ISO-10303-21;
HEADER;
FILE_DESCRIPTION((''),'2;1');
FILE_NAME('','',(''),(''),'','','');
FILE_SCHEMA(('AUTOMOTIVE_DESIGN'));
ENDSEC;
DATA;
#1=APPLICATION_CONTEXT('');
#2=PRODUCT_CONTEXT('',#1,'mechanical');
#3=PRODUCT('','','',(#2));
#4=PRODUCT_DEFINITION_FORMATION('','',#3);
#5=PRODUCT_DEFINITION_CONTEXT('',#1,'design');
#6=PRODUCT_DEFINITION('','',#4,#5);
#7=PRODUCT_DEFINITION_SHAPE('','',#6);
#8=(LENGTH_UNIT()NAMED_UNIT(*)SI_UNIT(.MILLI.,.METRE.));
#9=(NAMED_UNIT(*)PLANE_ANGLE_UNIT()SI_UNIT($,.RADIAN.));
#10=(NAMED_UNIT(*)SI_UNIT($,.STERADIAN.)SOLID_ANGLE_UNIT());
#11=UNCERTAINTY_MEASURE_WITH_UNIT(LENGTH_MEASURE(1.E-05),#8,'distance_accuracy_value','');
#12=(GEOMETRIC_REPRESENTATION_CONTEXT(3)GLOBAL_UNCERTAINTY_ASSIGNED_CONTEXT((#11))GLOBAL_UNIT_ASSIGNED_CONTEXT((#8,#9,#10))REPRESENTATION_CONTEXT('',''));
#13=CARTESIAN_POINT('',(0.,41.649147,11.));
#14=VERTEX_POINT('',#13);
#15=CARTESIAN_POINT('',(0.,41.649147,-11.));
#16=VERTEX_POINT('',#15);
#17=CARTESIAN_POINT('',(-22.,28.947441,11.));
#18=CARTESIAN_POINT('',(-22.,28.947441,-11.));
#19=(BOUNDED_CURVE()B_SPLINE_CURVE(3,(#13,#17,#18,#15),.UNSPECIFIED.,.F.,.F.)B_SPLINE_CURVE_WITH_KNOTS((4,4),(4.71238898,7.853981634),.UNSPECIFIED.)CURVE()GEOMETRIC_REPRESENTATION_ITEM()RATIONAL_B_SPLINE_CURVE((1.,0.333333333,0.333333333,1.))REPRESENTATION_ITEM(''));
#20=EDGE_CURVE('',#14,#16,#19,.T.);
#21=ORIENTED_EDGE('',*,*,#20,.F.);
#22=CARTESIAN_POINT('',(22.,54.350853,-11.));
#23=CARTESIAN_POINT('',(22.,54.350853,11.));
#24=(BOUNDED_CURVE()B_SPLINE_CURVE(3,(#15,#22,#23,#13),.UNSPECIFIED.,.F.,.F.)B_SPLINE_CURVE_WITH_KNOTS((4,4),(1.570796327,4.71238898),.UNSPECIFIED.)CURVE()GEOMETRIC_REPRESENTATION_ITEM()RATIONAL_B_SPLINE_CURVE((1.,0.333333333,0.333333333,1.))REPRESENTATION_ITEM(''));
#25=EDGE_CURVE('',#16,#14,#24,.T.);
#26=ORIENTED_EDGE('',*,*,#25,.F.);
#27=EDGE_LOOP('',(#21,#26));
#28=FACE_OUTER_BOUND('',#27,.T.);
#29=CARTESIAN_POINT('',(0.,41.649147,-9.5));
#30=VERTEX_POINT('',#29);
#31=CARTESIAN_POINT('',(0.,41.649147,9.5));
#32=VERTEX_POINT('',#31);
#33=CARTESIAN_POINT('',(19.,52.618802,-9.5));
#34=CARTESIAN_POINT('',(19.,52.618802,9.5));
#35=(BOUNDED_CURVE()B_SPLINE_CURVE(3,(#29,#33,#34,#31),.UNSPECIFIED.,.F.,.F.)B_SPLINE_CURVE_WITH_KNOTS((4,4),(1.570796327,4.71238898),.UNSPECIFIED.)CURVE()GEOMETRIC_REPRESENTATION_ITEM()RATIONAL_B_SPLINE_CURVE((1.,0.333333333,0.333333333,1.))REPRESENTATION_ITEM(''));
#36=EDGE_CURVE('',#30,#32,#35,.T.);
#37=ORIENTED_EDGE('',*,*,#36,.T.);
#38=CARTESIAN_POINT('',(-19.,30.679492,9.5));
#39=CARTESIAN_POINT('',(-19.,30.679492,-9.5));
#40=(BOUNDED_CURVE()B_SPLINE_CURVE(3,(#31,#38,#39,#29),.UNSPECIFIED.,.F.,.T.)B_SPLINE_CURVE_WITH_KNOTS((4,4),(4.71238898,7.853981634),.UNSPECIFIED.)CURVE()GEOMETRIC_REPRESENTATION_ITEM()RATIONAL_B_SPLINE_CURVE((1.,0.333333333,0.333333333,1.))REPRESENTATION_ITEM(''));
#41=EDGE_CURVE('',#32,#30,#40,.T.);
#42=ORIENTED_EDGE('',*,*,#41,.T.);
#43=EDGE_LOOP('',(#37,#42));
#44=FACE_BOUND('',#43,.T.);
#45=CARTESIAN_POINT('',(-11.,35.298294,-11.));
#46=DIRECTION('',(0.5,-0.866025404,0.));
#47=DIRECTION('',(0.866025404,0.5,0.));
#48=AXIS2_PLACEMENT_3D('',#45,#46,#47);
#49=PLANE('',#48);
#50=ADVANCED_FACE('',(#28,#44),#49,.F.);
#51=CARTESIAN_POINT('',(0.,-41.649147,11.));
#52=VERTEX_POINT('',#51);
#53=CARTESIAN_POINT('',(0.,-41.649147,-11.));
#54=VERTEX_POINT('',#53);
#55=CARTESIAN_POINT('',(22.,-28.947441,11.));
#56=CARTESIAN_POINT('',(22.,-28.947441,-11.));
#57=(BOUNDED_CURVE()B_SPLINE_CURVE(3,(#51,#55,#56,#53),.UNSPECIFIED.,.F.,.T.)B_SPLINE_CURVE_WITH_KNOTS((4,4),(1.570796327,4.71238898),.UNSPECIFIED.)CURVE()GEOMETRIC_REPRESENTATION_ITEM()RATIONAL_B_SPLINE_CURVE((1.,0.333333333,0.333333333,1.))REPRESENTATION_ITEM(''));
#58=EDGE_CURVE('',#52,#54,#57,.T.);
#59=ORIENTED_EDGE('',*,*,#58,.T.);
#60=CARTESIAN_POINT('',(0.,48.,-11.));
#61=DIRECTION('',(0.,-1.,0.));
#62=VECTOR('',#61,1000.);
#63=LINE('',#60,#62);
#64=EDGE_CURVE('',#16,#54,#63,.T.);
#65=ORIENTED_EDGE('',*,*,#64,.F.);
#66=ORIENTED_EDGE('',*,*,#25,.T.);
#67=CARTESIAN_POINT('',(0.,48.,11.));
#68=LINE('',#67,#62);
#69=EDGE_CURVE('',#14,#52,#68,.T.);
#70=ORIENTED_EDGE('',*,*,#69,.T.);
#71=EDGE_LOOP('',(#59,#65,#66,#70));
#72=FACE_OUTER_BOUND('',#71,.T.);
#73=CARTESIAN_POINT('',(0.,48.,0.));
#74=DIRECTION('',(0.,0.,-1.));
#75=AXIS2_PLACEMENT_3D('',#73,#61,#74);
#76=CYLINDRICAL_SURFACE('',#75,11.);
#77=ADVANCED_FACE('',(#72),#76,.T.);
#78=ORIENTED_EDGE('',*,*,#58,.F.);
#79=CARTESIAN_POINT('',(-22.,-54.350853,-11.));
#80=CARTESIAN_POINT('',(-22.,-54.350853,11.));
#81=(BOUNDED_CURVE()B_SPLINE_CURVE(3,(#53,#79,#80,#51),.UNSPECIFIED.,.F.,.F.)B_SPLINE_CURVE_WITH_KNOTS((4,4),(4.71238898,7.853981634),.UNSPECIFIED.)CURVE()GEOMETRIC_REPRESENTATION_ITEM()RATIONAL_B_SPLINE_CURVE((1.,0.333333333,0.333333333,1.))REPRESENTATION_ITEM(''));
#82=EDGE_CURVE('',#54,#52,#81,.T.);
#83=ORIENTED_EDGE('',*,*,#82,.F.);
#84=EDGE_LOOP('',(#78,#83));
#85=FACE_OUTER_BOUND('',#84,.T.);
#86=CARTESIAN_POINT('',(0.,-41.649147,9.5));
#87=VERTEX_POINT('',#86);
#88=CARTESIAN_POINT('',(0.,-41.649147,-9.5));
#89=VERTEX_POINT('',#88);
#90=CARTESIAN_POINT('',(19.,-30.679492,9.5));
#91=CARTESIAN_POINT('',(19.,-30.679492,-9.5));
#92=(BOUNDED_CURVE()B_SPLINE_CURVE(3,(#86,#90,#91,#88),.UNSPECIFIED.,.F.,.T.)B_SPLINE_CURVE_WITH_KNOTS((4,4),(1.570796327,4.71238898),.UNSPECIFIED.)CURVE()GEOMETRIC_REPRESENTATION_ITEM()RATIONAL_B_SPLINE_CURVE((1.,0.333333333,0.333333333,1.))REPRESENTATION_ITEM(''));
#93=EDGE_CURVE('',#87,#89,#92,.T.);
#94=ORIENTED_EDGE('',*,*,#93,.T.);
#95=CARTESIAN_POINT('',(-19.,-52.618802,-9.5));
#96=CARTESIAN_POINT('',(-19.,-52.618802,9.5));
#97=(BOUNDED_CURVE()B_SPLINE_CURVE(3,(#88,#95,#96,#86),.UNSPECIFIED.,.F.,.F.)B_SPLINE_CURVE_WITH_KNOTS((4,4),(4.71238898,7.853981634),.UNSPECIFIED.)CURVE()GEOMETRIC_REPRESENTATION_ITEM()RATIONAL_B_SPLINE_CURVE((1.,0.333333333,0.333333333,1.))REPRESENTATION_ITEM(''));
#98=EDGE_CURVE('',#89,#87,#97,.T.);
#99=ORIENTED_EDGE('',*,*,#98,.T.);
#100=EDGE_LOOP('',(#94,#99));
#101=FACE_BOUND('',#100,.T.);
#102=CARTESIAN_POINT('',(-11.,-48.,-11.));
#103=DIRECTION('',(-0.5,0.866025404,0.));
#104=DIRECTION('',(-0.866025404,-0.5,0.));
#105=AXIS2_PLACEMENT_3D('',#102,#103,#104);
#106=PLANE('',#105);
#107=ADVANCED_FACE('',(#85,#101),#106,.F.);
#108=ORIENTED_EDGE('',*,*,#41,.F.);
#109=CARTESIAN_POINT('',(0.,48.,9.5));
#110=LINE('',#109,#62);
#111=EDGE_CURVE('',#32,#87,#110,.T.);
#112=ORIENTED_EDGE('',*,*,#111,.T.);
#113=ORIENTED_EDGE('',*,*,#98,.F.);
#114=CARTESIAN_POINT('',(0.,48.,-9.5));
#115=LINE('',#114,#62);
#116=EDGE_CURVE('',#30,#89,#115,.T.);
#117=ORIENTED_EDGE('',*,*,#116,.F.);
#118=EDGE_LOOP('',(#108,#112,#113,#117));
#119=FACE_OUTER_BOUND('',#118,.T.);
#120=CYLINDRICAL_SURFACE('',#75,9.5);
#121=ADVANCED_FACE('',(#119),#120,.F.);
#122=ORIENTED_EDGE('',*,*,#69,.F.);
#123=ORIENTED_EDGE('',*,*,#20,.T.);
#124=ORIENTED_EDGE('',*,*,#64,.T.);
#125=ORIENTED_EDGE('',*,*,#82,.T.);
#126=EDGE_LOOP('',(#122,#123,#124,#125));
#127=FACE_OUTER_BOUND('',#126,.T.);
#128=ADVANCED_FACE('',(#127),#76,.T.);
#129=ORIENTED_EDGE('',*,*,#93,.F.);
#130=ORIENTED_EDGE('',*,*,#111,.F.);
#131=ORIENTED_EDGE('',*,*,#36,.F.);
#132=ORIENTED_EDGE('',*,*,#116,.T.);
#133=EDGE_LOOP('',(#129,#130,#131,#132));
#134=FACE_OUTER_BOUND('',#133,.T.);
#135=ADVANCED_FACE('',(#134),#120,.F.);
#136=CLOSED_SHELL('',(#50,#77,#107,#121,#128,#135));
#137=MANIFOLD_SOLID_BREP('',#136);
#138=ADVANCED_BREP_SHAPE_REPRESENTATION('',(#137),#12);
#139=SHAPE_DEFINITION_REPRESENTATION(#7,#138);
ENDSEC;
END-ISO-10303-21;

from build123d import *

# Parameters (mm, degrees)
SKETCH1_R               = 11
SKETCH1_R_2             = 9.5
BOSS_EXTRUDE1_DEPTH     = 48
CUT_EXTRUDE1_DEPTH      = 51.457903246
CUT_EXTRUDE1_DEPTH_BACK = 51.457903246


with BuildPart() as part:
    # Sketch1 → Boss-Extrude1 (new, symmetric)
    with BuildSketch(Plane(origin=(0, 0, 0), x_dir=(1, 0, 0), z_dir=(0, 1, 0))):
        with Locations(Location((0, 0, 0), (0, 0, 270))):
            Circle(SKETCH1_R)
        with Locations(Location((0, 0, 0), (0, 0, 270))):
            Circle(SKETCH1_R_2, mode=Mode.SUBTRACT)
    extrude(amount=BOSS_EXTRUDE1_DEPTH, both=True)

    # Sketch2 → Cut-Extrude1 (cut, two sides: drawn at the far end of the back side and taken through both)
    with BuildSketch(Plane.XY.offset(-CUT_EXTRUDE1_DEPTH_BACK)):
        Polygon((11, 48), (-11, 48), (-11, 35.298294078), align=None)
        Polygon((11, -35.298294078), (11, -48), (-11, -48), align=None)
    extrude(amount=CUT_EXTRUDE1_DEPTH + CUT_EXTRUDE1_DEPTH_BACK, mode=Mode.SUBTRACT)


solid = part.part
